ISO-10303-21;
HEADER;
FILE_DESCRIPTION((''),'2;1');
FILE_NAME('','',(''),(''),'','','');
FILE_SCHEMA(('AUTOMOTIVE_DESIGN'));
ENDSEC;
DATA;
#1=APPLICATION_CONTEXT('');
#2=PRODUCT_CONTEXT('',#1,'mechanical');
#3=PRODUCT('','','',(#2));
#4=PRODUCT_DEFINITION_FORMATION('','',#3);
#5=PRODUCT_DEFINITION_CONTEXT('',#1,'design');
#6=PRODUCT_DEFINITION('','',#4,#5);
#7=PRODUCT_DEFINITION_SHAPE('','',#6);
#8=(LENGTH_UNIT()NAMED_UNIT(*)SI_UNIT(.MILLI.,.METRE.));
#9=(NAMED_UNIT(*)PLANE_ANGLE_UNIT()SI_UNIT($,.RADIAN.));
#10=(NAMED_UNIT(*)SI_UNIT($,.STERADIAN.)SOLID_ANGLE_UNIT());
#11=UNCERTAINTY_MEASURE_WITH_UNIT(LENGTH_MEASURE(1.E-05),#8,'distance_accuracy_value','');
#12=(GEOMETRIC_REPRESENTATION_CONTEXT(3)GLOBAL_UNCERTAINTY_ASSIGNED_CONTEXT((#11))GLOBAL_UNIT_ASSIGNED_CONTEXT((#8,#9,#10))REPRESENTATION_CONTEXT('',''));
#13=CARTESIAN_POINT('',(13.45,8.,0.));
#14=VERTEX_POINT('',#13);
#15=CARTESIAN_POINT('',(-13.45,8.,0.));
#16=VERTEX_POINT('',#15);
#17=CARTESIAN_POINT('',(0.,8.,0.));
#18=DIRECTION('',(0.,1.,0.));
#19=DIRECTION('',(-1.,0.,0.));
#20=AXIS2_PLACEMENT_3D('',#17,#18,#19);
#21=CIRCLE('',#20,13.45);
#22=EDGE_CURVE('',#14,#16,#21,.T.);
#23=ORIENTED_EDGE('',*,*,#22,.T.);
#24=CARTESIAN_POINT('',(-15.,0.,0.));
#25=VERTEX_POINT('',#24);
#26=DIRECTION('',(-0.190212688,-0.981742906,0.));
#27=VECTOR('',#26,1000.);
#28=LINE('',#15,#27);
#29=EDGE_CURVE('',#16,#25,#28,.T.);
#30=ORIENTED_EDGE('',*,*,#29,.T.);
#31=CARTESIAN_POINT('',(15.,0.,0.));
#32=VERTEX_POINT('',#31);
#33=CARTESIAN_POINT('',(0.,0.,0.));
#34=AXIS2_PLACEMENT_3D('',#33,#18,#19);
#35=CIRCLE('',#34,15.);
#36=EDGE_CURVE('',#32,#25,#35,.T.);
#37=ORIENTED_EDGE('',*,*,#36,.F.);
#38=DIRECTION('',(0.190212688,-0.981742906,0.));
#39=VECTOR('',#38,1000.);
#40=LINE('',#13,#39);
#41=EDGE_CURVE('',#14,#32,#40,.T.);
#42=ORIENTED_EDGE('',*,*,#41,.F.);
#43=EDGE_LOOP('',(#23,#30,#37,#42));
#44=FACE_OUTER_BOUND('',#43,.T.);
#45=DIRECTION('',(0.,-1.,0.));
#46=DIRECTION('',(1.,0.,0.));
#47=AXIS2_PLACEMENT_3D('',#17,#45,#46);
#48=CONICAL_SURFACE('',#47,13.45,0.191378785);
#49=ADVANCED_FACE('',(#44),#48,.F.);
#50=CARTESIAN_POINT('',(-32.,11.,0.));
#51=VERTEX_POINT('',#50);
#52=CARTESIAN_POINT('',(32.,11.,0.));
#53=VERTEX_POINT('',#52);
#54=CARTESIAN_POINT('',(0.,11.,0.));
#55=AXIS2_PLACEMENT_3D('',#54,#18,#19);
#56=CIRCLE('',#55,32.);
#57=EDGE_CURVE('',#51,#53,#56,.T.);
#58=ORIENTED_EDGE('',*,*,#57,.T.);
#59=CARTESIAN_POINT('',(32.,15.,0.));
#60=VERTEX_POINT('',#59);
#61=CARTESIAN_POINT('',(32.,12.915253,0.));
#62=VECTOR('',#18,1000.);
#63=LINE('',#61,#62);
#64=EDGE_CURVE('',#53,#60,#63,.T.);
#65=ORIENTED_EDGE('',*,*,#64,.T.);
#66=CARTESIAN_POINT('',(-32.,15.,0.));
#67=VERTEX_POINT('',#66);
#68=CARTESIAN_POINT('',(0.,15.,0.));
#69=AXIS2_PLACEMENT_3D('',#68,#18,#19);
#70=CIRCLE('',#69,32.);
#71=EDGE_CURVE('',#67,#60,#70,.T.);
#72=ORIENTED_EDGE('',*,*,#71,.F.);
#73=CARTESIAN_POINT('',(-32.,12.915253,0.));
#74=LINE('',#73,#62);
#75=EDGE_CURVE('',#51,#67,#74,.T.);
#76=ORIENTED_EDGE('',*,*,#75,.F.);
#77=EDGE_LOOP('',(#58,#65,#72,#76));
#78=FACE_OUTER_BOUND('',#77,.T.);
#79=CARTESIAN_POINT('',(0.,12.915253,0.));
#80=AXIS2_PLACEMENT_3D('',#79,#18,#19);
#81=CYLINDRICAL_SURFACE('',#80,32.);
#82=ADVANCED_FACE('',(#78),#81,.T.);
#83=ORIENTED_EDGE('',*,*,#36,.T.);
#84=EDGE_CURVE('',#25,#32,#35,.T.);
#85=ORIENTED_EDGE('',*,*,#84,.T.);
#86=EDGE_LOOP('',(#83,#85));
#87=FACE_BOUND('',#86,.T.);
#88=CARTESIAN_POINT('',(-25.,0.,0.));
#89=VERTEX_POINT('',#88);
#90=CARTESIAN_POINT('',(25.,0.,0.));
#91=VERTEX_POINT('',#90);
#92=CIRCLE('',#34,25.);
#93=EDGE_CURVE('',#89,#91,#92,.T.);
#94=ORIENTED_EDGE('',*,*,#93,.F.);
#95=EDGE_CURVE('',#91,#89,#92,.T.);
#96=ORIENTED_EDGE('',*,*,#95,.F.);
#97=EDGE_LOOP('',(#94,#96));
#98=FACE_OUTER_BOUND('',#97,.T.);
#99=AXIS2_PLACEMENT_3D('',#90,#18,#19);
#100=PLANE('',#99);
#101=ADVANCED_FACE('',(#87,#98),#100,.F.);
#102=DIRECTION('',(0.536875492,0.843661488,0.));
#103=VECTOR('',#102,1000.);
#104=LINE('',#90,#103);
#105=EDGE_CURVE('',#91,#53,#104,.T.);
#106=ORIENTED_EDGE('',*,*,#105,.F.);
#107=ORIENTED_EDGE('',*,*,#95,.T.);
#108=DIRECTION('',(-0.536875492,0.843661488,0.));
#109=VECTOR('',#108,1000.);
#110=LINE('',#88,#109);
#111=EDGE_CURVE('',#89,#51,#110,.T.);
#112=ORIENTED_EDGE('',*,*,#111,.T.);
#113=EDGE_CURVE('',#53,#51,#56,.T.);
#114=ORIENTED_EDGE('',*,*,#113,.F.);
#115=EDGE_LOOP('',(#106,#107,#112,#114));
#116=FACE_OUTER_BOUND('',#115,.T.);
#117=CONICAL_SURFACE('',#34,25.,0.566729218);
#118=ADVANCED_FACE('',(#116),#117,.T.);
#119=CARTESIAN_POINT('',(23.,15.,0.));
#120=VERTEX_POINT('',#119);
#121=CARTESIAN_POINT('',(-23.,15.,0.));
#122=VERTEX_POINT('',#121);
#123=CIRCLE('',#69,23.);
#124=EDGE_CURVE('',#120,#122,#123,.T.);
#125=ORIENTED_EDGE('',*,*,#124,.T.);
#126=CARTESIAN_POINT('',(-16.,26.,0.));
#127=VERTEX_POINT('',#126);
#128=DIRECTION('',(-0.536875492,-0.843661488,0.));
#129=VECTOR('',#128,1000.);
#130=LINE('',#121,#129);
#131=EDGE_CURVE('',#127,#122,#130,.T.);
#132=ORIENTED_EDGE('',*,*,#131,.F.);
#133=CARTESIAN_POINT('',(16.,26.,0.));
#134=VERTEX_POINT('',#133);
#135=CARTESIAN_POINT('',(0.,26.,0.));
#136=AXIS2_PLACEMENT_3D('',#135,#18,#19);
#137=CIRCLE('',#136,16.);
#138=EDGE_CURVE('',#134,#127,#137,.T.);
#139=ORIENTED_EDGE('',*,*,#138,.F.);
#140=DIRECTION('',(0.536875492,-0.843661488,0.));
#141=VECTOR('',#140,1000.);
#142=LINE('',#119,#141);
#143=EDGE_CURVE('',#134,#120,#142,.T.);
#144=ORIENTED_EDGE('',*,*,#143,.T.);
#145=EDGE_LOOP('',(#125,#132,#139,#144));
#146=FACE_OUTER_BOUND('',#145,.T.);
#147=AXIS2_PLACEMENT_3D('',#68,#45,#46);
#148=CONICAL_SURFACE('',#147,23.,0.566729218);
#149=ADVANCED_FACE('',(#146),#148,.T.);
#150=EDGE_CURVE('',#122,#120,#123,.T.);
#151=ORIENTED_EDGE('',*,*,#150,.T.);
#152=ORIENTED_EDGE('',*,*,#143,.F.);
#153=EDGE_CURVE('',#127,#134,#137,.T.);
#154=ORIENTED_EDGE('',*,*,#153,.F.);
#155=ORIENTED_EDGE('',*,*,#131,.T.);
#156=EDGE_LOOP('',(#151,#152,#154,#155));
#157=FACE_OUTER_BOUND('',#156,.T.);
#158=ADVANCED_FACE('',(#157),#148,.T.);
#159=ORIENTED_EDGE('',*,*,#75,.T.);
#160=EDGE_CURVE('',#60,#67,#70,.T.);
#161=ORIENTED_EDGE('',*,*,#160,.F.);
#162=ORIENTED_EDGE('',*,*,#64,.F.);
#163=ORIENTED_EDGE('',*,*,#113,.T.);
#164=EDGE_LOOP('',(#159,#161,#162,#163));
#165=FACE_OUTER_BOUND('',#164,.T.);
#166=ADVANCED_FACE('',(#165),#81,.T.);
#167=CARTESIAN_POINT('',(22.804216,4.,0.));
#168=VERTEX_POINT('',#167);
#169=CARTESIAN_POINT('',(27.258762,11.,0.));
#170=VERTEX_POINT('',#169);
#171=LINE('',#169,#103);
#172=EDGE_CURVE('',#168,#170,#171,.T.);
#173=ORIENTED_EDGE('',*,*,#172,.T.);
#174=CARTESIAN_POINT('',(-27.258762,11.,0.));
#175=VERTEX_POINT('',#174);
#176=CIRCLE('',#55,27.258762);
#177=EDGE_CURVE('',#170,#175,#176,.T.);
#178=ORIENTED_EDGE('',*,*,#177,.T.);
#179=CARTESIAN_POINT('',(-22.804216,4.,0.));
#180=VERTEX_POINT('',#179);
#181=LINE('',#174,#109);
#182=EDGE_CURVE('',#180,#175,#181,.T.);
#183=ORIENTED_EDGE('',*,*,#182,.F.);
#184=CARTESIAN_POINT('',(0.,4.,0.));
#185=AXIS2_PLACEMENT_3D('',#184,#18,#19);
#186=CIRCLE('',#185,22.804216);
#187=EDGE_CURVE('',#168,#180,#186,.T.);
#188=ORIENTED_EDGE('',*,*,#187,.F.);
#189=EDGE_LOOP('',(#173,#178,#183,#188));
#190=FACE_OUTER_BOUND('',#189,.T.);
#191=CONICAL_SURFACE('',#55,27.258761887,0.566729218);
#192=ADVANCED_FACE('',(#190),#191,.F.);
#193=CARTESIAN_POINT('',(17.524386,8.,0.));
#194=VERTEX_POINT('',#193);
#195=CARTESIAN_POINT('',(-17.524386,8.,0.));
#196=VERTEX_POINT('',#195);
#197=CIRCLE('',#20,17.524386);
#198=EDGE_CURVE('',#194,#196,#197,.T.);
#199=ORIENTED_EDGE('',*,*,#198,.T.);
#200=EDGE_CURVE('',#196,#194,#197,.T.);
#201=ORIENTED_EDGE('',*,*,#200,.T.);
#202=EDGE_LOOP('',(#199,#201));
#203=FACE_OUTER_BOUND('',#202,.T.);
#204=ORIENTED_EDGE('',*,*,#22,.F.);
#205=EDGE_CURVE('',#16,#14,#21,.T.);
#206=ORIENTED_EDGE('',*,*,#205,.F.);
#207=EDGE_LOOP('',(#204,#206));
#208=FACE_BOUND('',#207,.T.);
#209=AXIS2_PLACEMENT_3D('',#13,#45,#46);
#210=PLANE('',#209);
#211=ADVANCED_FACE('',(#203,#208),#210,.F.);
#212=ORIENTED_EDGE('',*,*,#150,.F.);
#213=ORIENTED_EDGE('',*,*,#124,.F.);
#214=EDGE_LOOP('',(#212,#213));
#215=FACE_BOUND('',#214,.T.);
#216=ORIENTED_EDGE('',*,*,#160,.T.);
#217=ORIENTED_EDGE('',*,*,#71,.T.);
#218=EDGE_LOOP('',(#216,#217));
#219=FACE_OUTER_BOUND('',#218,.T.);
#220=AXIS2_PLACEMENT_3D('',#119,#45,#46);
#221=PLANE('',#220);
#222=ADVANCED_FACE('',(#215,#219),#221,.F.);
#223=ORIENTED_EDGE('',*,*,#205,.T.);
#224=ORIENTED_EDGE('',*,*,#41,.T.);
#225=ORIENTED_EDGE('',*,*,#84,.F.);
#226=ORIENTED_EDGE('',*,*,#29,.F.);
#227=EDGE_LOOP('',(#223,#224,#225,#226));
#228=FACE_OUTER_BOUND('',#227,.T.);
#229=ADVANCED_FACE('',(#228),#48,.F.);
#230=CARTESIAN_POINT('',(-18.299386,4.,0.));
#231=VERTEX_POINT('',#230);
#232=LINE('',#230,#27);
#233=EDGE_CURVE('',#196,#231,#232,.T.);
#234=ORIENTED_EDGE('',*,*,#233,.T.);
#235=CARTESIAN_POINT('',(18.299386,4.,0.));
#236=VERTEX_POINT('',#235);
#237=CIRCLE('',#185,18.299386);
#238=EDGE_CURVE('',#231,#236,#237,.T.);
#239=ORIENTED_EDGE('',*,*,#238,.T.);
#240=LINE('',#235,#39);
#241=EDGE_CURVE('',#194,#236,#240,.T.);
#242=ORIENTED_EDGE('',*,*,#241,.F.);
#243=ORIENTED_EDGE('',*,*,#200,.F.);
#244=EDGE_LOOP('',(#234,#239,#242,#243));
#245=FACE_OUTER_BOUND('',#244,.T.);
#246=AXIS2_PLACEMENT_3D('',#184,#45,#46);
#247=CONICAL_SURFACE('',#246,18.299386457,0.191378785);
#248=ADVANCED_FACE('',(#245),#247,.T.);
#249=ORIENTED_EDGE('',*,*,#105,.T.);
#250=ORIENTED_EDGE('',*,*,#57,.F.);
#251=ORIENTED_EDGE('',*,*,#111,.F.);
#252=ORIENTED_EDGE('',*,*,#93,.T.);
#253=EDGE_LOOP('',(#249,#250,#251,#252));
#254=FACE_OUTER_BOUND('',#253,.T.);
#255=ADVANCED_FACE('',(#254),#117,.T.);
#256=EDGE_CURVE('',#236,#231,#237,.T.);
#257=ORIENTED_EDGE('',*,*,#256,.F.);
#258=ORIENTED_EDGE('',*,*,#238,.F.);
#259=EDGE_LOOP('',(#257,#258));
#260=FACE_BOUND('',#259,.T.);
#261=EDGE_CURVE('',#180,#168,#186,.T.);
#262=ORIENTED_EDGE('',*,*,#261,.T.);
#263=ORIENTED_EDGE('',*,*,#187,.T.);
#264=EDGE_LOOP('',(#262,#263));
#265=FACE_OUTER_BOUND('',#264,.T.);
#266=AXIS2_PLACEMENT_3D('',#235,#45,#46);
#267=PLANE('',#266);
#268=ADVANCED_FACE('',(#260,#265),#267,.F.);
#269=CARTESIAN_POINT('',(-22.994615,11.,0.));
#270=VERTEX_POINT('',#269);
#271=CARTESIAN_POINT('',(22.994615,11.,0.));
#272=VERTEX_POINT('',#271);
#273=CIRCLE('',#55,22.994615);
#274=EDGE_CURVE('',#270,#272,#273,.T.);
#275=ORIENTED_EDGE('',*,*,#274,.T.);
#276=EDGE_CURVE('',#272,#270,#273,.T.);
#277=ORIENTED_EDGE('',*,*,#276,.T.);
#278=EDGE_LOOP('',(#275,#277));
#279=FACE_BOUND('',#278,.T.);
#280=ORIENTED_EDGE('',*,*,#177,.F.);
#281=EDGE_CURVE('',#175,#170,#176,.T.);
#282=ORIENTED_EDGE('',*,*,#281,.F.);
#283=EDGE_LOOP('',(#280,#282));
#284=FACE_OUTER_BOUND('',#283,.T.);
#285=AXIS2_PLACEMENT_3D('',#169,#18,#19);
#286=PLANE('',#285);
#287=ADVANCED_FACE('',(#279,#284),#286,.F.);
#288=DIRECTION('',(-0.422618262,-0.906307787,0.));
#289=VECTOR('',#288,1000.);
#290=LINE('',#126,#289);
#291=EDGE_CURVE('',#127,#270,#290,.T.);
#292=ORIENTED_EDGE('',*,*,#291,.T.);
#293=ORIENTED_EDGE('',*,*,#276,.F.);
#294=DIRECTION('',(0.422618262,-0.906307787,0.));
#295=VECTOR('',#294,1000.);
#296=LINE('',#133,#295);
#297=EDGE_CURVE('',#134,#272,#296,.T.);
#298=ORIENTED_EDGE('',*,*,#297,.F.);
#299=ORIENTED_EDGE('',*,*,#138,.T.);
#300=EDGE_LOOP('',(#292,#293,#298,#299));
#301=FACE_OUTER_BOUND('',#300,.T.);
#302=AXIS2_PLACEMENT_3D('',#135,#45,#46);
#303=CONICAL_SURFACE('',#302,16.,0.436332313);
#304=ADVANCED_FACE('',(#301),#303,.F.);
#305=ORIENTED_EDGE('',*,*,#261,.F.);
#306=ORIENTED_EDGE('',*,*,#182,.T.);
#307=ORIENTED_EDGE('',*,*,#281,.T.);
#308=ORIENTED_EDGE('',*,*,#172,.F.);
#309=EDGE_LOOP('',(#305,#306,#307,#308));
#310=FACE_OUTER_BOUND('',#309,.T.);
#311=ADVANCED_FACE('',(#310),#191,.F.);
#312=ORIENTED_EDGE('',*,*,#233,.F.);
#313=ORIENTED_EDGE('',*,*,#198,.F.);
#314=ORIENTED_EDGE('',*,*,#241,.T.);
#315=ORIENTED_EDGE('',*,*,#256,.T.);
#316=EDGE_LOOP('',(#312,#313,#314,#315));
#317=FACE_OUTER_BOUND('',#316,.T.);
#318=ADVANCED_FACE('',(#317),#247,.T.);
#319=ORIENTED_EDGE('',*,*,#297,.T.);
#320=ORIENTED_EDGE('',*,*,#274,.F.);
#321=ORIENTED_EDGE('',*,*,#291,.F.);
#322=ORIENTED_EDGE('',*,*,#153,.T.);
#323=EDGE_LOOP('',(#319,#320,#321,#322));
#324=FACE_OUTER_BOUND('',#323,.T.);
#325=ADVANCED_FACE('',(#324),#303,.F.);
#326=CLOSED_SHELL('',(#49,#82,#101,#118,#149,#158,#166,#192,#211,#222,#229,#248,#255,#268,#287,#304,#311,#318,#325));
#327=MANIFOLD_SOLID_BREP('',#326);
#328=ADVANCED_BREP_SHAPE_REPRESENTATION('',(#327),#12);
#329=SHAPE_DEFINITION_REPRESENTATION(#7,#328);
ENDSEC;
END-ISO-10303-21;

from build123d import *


with BuildPart() as part:
    # Sketch1 → Revolve1 (revolve)
    with BuildSketch(Plane.XY, mode=Mode.PRIVATE) as revolve1_sk:
        Polygon((16, 26), (23, 15), (32, 15), (32, 11), (25, 0), (15, 0), (13.45, 8), (17.524386457, 8), (18.299386457, 4), (22.804216433, 4), (27.258761887, 11), (22.994614872, 11), align=None)
    revolve(revolve1_sk.sketch.rotate(Axis((0, 12.915252942, 0), (0, -1, 0)), 180), axis=Axis((0, 12.915252942, 0), (0, -1, 0)))


solid = part.part
